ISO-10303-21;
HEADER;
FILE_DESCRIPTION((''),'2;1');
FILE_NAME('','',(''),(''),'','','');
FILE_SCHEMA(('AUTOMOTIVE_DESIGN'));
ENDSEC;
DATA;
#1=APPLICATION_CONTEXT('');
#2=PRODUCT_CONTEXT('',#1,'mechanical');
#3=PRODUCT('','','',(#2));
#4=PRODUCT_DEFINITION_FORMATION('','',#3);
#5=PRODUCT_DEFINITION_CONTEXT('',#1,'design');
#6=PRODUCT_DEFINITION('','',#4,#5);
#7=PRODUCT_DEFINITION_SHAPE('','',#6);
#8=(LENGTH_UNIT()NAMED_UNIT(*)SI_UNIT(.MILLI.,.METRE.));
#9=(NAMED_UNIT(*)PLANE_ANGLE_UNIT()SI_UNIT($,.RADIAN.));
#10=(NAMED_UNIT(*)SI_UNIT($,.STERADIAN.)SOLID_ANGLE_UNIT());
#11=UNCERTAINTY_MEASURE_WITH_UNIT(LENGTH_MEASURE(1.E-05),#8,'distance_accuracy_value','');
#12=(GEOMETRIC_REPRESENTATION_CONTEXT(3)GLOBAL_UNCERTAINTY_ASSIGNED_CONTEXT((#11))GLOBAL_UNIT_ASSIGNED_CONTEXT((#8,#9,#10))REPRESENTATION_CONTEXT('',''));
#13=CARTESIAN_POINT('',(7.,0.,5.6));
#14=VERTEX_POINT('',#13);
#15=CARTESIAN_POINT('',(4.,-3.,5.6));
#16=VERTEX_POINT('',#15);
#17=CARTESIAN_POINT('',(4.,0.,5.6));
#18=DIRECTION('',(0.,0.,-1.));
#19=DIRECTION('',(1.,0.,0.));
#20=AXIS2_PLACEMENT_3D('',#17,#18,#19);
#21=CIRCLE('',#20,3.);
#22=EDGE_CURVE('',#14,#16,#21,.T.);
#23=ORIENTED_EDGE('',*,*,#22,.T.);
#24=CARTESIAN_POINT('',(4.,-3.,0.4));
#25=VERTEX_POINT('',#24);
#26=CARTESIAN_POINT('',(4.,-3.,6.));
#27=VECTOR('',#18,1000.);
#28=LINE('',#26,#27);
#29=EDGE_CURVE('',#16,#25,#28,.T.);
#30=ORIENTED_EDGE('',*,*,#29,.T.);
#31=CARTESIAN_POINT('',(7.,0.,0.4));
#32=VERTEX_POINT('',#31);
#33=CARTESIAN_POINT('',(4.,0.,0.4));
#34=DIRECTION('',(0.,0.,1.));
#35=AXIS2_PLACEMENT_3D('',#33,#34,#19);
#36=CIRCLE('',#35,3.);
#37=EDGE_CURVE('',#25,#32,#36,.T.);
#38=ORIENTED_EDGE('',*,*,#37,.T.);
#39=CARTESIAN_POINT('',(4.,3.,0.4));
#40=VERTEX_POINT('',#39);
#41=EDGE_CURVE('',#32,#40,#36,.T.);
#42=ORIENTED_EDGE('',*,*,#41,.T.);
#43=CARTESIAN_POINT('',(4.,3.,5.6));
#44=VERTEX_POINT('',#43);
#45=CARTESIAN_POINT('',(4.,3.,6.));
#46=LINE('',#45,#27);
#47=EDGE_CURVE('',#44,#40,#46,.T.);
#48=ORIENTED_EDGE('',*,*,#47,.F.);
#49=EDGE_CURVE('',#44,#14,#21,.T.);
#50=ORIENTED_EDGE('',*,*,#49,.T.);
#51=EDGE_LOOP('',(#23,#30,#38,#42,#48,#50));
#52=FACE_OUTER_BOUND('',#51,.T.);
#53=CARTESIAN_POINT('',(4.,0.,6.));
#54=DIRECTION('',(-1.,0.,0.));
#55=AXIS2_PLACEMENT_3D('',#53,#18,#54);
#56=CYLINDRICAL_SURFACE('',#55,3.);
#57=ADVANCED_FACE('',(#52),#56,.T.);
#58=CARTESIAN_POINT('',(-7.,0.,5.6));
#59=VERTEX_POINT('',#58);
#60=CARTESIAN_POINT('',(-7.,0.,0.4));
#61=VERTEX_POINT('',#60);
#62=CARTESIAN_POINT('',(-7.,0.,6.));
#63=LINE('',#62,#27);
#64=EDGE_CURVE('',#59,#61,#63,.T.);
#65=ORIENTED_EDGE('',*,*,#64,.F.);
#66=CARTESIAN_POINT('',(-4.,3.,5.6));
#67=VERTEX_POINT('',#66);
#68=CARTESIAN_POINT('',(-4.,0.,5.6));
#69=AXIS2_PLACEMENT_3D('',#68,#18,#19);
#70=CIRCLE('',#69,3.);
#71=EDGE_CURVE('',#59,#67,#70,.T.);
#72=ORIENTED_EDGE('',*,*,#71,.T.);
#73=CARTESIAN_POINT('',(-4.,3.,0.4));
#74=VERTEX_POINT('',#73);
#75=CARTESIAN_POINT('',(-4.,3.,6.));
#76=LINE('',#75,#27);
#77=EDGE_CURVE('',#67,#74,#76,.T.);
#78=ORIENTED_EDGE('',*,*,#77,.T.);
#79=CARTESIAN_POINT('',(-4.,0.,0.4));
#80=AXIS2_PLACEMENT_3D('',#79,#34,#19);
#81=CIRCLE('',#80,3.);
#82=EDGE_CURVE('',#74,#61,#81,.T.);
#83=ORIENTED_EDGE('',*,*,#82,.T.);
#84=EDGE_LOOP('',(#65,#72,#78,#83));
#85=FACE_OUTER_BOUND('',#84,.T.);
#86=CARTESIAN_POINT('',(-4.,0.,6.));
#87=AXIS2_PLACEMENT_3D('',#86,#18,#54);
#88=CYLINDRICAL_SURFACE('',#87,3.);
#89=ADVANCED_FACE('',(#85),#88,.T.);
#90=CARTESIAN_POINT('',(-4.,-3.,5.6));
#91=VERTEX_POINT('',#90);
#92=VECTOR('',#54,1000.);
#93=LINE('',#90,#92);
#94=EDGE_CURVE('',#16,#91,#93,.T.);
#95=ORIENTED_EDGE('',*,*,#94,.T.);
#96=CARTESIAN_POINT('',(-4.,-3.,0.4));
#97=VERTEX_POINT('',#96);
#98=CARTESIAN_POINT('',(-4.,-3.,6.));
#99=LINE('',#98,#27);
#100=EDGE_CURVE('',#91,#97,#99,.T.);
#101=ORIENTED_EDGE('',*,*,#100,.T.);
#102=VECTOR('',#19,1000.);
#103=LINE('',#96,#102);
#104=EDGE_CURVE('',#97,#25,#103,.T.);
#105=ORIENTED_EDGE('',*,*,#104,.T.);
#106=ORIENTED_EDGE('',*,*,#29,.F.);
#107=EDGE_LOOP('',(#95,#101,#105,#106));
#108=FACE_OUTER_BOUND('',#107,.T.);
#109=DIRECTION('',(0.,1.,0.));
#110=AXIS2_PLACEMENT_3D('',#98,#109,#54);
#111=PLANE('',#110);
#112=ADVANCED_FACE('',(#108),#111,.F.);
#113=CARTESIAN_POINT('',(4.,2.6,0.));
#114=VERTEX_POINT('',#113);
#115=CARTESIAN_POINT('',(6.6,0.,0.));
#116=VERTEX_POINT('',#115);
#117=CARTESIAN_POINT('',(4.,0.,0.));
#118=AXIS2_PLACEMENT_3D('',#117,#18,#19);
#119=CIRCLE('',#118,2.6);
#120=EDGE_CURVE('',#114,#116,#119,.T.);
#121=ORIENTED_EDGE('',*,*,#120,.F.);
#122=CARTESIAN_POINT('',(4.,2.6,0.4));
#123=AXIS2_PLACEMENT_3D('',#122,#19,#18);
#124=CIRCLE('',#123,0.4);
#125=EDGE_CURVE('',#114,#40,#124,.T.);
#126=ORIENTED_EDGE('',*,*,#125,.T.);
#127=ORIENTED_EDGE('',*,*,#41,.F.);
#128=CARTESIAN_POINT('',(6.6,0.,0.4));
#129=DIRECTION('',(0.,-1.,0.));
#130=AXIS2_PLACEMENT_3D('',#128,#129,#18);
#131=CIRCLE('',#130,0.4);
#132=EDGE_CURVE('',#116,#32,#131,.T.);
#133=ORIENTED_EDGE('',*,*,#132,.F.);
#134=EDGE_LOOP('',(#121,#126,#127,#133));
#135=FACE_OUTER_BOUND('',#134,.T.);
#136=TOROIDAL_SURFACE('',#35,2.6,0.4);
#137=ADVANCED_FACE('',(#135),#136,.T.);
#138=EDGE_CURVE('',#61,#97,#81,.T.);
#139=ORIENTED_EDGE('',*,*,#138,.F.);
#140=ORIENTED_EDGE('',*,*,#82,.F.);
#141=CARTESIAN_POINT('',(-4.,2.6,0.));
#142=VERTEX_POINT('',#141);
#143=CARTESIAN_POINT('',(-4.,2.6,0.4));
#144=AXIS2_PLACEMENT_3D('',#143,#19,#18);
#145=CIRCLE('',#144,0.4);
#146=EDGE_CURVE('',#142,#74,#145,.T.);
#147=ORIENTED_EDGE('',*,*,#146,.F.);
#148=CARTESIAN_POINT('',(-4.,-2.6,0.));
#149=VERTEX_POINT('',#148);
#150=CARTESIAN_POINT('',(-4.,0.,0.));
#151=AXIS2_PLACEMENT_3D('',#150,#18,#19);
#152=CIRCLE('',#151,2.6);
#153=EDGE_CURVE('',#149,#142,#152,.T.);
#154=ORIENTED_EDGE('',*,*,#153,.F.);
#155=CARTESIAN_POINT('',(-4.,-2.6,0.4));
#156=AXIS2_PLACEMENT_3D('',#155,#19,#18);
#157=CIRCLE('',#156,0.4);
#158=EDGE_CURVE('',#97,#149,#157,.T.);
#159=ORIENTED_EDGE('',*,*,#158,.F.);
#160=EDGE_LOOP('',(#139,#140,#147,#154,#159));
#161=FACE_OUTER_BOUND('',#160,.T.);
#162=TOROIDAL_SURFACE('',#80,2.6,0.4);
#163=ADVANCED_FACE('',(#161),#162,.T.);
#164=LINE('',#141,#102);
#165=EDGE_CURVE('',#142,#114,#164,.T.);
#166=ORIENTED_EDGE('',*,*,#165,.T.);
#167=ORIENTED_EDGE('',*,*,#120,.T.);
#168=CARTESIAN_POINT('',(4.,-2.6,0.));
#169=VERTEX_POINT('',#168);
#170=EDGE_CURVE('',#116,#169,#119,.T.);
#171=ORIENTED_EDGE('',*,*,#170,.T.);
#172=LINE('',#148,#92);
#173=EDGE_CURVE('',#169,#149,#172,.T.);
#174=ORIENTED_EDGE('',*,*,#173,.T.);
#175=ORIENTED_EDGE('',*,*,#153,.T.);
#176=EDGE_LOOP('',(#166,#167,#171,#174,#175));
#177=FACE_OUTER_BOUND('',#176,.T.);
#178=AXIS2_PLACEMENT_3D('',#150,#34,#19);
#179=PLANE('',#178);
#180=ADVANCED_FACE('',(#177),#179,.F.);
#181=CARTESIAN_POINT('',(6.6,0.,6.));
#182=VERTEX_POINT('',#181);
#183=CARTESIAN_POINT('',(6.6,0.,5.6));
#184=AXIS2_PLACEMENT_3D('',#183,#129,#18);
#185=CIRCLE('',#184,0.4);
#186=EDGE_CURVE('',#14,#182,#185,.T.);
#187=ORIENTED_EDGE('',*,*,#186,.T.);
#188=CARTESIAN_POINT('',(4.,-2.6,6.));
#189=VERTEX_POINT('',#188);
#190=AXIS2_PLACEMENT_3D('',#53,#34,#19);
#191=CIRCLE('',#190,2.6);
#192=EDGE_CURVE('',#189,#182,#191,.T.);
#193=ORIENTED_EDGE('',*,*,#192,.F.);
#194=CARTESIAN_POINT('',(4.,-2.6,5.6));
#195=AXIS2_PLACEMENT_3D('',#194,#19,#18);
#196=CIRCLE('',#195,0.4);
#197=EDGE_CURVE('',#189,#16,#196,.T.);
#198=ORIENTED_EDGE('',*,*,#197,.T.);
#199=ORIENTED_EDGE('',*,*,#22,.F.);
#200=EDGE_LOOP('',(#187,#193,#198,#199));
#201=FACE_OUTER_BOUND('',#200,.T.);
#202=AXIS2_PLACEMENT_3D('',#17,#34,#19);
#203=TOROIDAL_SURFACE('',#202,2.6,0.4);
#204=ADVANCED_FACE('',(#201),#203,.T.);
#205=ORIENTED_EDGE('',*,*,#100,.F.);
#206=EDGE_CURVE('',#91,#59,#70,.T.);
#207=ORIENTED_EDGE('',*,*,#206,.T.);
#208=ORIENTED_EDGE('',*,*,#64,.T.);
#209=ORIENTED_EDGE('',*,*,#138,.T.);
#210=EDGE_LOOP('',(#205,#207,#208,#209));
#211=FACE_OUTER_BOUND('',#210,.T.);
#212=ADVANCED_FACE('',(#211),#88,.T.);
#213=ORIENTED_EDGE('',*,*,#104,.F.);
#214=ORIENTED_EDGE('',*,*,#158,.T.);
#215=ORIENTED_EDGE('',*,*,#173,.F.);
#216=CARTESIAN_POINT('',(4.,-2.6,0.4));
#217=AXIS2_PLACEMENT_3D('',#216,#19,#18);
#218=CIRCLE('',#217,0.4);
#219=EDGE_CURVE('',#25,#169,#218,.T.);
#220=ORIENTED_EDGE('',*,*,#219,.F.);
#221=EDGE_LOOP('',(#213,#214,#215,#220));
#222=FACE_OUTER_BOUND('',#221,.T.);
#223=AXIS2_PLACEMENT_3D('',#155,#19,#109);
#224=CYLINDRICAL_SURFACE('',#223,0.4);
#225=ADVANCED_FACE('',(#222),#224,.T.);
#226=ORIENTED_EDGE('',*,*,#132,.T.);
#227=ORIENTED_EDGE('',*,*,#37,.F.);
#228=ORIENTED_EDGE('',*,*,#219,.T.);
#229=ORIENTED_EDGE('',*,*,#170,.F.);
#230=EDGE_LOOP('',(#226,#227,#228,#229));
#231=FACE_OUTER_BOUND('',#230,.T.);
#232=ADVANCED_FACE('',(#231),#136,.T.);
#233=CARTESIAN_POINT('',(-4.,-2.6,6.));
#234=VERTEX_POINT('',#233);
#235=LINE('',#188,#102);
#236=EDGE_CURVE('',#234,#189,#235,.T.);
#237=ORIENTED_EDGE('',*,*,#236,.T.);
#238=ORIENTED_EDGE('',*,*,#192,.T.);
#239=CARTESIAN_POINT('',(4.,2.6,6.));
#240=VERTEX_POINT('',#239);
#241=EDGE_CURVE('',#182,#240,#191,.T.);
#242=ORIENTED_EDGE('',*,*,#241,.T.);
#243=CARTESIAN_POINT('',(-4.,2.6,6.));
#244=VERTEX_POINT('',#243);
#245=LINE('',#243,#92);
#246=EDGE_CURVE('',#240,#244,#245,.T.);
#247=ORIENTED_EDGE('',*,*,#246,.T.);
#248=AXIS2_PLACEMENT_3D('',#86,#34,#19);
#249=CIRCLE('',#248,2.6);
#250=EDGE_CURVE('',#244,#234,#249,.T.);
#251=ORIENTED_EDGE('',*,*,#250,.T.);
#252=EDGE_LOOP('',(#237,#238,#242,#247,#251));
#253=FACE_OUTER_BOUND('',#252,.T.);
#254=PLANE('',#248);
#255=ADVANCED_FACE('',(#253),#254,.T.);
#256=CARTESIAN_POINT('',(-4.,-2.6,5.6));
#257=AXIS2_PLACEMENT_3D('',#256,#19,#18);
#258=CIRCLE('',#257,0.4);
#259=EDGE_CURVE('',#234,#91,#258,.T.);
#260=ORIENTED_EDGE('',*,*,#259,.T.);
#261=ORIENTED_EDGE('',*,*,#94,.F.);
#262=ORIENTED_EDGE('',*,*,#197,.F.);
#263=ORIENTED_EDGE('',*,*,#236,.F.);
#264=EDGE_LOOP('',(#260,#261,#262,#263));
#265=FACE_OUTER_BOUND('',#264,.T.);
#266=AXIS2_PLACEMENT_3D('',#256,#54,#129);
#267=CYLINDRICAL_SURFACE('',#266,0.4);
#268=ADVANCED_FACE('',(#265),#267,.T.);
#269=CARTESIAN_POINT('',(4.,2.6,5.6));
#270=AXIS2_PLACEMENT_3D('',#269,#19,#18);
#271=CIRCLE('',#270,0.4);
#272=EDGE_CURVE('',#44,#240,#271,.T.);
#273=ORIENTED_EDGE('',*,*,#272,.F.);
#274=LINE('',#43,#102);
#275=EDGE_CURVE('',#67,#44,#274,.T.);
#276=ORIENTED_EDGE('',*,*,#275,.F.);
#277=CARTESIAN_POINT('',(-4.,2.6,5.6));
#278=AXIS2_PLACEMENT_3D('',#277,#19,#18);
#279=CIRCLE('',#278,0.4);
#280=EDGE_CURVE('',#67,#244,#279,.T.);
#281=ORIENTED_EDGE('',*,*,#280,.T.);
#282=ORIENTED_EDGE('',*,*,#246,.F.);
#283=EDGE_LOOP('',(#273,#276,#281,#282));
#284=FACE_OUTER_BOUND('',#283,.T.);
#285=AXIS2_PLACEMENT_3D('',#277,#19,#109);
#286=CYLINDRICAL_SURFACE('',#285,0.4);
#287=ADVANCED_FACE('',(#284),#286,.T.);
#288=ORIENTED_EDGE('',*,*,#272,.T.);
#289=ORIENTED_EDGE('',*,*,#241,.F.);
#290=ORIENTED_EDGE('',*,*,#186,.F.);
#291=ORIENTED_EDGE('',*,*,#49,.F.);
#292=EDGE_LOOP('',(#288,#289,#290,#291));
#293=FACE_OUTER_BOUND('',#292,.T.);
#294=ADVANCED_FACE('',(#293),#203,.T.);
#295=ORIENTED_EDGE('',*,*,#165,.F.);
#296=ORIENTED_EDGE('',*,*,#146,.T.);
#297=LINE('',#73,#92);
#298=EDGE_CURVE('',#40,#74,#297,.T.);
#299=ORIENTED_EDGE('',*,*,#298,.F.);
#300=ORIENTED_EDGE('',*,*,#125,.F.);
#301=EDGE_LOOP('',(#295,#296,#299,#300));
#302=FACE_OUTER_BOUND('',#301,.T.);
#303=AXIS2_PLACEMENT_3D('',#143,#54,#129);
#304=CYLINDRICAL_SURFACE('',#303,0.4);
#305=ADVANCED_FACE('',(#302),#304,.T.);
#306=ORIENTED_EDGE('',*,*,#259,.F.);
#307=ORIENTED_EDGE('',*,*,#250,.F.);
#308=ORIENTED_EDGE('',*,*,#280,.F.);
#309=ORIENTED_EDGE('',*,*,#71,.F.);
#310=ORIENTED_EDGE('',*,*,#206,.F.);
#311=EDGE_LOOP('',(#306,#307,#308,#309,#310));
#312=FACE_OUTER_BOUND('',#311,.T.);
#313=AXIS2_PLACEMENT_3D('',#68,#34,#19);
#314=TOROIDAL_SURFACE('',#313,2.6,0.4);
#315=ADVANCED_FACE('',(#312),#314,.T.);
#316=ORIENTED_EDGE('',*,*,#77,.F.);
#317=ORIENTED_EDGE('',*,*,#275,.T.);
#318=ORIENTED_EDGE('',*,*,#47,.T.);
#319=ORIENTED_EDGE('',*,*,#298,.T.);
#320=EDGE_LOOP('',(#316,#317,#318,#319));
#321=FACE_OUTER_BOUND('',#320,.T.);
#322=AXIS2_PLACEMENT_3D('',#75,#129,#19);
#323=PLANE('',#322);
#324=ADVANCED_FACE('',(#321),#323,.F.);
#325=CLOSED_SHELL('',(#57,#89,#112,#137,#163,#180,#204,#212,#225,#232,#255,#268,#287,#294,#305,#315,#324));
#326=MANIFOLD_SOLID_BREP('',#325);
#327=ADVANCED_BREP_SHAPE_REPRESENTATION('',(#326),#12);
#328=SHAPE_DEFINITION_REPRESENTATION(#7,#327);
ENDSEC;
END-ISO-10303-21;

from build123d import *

# Parameters (mm, degrees)
EXTRUDE_523_DEPTH = 6
FILLET_1_R        = 0.4


with BuildPart() as part:
    # 草图1 → Extrude 523 (new body)
    with BuildSketch(Plane.XY):
        with BuildLine():
            Line((-4, 3), (4, 3))
            ThreePointArc((4, 3), (7, 0), (4, -3))
            Line((4, -3), (-4, -3))
            ThreePointArc((-4, -3), (-7, 0), (-4, 3))
        make_face()
    extrude(amount=EXTRUDE_523_DEPTH)

    # 圆角1
    fillet_1_edges = [part.edges().sort_by_distance(p)[0] for p in [
        (7, 0, 6),
        (0, 3, 6),
        (-7, 0, 6),
        (0, 3, 0),
        (7, 0, 0),
        (0, -3, 0),
        (-7, 0, 0),
        (0, -3, 6),
    ]]
    fillet(fillet_1_edges, radius=FILLET_1_R)


solid = part.part
